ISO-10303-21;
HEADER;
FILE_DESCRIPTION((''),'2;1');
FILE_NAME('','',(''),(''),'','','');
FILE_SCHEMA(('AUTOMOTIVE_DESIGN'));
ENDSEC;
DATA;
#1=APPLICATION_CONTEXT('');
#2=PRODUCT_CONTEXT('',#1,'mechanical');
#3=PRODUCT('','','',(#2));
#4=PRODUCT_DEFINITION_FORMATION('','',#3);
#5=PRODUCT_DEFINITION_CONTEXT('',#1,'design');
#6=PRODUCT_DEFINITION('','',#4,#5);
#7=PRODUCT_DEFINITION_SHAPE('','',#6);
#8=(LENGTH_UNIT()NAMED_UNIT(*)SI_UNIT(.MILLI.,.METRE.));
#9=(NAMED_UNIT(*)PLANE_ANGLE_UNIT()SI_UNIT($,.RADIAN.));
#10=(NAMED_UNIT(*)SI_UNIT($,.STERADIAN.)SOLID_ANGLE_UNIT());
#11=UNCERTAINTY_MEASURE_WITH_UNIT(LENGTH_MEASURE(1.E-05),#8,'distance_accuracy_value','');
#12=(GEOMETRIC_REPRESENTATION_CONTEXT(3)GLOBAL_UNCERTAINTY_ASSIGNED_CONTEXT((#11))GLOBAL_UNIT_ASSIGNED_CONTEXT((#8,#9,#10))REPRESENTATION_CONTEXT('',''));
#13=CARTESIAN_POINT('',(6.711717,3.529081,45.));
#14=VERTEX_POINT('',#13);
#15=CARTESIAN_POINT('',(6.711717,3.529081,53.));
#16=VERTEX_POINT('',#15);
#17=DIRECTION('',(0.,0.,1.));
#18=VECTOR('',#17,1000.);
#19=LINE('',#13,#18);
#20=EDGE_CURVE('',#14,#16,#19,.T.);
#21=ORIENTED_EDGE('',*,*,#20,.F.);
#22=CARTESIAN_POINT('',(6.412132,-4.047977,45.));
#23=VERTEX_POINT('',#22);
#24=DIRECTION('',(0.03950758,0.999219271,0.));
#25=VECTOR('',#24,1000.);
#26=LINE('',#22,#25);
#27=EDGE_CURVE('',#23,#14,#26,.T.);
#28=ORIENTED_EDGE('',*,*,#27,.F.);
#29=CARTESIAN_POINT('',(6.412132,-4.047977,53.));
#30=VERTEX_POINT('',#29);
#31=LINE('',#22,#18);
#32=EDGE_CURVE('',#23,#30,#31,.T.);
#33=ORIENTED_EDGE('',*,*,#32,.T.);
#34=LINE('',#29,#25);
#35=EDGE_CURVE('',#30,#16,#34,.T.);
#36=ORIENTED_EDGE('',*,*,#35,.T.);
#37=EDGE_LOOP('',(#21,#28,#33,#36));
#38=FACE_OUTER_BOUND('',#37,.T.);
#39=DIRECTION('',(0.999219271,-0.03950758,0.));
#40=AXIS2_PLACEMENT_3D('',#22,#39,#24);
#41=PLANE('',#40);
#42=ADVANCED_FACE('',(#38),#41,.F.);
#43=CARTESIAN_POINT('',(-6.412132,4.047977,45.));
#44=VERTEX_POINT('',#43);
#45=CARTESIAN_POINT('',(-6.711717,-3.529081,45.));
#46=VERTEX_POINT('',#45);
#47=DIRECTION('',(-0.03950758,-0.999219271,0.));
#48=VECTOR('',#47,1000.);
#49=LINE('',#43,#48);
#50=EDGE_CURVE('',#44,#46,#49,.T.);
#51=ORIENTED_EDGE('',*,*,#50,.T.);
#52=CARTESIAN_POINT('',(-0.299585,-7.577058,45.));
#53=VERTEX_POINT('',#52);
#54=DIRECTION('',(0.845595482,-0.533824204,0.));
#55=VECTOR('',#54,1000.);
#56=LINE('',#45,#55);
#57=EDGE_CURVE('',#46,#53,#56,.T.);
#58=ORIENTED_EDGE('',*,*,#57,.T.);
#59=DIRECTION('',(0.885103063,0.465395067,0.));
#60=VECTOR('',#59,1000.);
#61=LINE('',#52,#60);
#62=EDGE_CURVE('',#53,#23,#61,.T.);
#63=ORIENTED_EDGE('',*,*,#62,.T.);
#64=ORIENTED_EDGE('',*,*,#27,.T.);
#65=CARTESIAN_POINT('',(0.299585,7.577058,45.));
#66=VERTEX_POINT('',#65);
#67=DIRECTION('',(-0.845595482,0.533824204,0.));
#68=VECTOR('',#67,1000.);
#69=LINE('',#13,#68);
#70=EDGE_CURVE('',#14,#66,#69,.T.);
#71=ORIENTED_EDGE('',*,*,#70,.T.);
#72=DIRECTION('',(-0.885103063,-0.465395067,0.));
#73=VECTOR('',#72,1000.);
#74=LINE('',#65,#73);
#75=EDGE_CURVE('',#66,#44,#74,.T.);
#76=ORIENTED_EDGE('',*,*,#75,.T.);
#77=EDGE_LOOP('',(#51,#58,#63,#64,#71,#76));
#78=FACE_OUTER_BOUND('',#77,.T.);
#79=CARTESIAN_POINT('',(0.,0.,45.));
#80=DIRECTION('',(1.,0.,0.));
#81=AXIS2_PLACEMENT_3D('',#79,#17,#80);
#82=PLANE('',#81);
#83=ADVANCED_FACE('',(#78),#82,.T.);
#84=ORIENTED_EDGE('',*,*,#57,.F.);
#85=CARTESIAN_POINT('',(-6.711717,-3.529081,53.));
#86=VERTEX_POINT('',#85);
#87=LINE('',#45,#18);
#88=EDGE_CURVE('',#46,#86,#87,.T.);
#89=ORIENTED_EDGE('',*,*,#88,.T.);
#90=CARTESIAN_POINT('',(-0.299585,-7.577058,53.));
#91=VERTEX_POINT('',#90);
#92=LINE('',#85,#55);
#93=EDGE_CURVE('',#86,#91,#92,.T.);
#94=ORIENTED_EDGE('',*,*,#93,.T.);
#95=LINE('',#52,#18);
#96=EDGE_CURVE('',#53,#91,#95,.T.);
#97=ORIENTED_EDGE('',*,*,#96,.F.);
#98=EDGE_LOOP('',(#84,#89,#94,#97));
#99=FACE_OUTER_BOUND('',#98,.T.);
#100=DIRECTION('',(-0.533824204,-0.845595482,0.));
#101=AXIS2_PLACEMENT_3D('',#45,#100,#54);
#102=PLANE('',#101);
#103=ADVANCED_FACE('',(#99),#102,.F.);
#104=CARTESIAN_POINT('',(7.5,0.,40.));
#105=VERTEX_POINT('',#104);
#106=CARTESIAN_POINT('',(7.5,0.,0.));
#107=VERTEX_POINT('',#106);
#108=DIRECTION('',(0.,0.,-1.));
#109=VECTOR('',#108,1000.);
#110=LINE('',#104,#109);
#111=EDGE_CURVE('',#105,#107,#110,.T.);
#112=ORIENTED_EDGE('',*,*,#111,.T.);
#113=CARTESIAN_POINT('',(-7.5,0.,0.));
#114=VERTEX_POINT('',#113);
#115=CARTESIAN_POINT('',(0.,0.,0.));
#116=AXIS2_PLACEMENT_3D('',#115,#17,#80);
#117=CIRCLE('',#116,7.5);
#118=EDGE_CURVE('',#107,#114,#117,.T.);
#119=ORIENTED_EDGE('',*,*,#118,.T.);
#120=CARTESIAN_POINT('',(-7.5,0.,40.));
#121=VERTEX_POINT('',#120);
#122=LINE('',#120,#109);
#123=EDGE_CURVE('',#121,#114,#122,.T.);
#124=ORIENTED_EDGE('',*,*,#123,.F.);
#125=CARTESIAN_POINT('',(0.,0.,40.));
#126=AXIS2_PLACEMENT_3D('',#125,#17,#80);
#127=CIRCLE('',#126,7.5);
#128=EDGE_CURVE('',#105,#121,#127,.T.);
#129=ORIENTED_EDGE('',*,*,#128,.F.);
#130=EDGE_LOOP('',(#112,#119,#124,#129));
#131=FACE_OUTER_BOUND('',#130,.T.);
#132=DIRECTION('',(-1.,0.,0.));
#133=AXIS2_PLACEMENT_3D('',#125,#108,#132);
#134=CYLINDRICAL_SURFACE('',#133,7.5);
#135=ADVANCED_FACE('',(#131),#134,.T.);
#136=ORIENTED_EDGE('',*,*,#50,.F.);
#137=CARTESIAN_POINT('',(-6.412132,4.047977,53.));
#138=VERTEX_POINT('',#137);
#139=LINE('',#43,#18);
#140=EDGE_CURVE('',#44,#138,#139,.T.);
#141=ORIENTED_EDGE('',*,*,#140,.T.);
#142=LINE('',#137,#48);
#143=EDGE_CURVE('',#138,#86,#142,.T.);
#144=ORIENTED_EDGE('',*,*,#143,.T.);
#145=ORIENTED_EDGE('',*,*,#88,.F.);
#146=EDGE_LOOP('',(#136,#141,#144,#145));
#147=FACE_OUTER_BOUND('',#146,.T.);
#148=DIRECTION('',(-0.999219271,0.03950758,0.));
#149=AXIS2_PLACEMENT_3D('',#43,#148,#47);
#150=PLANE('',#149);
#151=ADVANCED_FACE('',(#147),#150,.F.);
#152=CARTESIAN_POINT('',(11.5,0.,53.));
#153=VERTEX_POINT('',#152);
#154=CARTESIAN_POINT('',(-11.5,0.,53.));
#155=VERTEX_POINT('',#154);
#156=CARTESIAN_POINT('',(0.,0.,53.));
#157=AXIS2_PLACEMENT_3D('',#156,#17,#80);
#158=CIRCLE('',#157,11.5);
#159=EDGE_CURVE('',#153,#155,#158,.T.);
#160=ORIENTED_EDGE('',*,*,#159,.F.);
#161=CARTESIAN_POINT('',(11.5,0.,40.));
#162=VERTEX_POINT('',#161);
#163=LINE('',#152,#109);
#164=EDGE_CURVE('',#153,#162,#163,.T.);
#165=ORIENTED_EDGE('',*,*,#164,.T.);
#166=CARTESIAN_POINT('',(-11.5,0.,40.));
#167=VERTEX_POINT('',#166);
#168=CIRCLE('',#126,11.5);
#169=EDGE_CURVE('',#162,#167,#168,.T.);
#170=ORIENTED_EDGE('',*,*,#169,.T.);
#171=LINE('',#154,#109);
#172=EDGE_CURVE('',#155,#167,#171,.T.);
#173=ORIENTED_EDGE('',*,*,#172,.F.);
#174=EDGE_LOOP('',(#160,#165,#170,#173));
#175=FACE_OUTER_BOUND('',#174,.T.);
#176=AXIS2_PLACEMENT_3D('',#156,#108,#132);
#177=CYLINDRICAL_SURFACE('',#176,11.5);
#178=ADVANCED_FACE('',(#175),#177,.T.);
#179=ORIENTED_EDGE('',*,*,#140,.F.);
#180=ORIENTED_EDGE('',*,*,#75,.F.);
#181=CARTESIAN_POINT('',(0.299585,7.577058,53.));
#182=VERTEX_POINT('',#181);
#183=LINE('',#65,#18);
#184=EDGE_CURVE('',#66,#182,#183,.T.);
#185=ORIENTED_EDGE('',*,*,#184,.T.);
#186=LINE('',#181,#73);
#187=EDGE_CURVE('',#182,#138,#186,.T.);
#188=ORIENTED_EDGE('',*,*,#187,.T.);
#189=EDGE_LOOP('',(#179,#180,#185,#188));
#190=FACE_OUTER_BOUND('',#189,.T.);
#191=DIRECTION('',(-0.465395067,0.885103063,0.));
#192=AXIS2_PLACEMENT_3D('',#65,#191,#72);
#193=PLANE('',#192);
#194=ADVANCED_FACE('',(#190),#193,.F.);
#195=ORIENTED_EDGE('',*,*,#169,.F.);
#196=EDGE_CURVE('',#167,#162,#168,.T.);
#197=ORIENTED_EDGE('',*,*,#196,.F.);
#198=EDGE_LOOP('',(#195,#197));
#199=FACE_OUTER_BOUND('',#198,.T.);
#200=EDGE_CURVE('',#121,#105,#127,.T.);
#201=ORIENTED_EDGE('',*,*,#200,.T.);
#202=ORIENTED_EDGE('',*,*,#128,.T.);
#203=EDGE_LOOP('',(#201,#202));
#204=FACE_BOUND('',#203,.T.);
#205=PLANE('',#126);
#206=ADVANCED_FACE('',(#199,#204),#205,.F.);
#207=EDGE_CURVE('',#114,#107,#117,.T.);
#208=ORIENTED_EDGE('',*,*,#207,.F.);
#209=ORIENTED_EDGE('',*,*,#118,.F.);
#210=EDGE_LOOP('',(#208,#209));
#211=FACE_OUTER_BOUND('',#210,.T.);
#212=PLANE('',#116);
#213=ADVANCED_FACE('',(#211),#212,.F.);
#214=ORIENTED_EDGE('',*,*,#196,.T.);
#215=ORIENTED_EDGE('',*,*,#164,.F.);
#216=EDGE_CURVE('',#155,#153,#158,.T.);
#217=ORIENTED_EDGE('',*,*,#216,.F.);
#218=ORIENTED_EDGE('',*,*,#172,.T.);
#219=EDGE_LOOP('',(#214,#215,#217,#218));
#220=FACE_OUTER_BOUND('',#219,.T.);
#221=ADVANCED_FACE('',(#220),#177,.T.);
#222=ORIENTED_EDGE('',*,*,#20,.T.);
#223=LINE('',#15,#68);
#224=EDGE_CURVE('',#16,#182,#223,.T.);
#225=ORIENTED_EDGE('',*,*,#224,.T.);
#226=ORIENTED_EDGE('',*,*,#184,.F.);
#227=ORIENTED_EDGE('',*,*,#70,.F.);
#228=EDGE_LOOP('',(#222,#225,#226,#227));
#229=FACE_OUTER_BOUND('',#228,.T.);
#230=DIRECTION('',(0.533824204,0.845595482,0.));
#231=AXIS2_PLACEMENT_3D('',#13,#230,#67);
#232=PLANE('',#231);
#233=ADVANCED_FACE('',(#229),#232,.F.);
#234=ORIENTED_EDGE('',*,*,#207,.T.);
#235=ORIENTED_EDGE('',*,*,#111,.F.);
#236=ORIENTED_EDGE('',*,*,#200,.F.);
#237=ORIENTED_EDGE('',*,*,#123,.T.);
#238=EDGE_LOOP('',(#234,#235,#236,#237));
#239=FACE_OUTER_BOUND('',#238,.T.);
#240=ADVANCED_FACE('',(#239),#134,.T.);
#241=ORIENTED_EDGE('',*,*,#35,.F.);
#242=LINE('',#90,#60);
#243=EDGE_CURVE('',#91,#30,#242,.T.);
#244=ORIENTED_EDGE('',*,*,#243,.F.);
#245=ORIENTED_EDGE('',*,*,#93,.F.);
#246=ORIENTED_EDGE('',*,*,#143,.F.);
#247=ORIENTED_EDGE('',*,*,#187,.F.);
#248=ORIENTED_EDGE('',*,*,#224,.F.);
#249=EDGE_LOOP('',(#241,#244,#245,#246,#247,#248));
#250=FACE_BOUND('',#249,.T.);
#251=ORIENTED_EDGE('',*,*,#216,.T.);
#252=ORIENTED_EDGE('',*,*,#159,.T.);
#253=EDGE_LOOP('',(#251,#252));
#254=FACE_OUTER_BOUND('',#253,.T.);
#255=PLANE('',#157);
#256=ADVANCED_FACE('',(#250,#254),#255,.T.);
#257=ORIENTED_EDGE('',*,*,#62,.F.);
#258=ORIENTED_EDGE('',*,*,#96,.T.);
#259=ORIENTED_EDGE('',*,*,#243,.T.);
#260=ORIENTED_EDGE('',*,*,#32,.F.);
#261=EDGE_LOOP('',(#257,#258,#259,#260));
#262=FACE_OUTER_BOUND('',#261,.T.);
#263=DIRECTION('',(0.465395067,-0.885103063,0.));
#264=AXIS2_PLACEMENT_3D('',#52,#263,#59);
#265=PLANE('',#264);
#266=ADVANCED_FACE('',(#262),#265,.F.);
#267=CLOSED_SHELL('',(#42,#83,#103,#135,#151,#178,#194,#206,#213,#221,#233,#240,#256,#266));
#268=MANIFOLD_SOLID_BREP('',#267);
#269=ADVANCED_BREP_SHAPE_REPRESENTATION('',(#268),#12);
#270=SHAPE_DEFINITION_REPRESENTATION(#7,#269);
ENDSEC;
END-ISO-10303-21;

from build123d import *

# Parameters (mm, degrees)
SKETCH1_R           = 7.5
BOSS_EXTRUDE1_DEPTH = 40
SKETCH2_R           = 11.5
BOSS_EXTRUDE2_DEPTH = 13
CUT_EXTRUDE1_DEPTH  = 8


with BuildPart() as part:
    # Sketch1 → Boss-Extrude1 (new body)
    with BuildSketch(Plane.XY):
        Circle(SKETCH1_R)
    extrude(amount=BOSS_EXTRUDE1_DEPTH)

    # Sketch2 → Boss-Extrude2 (add)
    with BuildSketch(Plane.XY.offset(40)):
        with Locations(Location((0, 0, 0), (0, 0, 180))):
            Circle(SKETCH2_R)
    extrude(amount=BOSS_EXTRUDE2_DEPTH)

    # Sketch3 → Cut-Extrude1 (cut)
    with BuildSketch(Plane.XY.offset(53)):
        Polygon((6.412132048, -4.047977261), (6.711717166, 3.529080616), (0.299585118, 7.577057877), (-6.412132048, 4.047977261), (-6.711717166, -3.529080616), (-0.299585118, -7.577057877), align=None)
    extrude(amount=-CUT_EXTRUDE1_DEPTH, mode=Mode.SUBTRACT)


solid = part.part
